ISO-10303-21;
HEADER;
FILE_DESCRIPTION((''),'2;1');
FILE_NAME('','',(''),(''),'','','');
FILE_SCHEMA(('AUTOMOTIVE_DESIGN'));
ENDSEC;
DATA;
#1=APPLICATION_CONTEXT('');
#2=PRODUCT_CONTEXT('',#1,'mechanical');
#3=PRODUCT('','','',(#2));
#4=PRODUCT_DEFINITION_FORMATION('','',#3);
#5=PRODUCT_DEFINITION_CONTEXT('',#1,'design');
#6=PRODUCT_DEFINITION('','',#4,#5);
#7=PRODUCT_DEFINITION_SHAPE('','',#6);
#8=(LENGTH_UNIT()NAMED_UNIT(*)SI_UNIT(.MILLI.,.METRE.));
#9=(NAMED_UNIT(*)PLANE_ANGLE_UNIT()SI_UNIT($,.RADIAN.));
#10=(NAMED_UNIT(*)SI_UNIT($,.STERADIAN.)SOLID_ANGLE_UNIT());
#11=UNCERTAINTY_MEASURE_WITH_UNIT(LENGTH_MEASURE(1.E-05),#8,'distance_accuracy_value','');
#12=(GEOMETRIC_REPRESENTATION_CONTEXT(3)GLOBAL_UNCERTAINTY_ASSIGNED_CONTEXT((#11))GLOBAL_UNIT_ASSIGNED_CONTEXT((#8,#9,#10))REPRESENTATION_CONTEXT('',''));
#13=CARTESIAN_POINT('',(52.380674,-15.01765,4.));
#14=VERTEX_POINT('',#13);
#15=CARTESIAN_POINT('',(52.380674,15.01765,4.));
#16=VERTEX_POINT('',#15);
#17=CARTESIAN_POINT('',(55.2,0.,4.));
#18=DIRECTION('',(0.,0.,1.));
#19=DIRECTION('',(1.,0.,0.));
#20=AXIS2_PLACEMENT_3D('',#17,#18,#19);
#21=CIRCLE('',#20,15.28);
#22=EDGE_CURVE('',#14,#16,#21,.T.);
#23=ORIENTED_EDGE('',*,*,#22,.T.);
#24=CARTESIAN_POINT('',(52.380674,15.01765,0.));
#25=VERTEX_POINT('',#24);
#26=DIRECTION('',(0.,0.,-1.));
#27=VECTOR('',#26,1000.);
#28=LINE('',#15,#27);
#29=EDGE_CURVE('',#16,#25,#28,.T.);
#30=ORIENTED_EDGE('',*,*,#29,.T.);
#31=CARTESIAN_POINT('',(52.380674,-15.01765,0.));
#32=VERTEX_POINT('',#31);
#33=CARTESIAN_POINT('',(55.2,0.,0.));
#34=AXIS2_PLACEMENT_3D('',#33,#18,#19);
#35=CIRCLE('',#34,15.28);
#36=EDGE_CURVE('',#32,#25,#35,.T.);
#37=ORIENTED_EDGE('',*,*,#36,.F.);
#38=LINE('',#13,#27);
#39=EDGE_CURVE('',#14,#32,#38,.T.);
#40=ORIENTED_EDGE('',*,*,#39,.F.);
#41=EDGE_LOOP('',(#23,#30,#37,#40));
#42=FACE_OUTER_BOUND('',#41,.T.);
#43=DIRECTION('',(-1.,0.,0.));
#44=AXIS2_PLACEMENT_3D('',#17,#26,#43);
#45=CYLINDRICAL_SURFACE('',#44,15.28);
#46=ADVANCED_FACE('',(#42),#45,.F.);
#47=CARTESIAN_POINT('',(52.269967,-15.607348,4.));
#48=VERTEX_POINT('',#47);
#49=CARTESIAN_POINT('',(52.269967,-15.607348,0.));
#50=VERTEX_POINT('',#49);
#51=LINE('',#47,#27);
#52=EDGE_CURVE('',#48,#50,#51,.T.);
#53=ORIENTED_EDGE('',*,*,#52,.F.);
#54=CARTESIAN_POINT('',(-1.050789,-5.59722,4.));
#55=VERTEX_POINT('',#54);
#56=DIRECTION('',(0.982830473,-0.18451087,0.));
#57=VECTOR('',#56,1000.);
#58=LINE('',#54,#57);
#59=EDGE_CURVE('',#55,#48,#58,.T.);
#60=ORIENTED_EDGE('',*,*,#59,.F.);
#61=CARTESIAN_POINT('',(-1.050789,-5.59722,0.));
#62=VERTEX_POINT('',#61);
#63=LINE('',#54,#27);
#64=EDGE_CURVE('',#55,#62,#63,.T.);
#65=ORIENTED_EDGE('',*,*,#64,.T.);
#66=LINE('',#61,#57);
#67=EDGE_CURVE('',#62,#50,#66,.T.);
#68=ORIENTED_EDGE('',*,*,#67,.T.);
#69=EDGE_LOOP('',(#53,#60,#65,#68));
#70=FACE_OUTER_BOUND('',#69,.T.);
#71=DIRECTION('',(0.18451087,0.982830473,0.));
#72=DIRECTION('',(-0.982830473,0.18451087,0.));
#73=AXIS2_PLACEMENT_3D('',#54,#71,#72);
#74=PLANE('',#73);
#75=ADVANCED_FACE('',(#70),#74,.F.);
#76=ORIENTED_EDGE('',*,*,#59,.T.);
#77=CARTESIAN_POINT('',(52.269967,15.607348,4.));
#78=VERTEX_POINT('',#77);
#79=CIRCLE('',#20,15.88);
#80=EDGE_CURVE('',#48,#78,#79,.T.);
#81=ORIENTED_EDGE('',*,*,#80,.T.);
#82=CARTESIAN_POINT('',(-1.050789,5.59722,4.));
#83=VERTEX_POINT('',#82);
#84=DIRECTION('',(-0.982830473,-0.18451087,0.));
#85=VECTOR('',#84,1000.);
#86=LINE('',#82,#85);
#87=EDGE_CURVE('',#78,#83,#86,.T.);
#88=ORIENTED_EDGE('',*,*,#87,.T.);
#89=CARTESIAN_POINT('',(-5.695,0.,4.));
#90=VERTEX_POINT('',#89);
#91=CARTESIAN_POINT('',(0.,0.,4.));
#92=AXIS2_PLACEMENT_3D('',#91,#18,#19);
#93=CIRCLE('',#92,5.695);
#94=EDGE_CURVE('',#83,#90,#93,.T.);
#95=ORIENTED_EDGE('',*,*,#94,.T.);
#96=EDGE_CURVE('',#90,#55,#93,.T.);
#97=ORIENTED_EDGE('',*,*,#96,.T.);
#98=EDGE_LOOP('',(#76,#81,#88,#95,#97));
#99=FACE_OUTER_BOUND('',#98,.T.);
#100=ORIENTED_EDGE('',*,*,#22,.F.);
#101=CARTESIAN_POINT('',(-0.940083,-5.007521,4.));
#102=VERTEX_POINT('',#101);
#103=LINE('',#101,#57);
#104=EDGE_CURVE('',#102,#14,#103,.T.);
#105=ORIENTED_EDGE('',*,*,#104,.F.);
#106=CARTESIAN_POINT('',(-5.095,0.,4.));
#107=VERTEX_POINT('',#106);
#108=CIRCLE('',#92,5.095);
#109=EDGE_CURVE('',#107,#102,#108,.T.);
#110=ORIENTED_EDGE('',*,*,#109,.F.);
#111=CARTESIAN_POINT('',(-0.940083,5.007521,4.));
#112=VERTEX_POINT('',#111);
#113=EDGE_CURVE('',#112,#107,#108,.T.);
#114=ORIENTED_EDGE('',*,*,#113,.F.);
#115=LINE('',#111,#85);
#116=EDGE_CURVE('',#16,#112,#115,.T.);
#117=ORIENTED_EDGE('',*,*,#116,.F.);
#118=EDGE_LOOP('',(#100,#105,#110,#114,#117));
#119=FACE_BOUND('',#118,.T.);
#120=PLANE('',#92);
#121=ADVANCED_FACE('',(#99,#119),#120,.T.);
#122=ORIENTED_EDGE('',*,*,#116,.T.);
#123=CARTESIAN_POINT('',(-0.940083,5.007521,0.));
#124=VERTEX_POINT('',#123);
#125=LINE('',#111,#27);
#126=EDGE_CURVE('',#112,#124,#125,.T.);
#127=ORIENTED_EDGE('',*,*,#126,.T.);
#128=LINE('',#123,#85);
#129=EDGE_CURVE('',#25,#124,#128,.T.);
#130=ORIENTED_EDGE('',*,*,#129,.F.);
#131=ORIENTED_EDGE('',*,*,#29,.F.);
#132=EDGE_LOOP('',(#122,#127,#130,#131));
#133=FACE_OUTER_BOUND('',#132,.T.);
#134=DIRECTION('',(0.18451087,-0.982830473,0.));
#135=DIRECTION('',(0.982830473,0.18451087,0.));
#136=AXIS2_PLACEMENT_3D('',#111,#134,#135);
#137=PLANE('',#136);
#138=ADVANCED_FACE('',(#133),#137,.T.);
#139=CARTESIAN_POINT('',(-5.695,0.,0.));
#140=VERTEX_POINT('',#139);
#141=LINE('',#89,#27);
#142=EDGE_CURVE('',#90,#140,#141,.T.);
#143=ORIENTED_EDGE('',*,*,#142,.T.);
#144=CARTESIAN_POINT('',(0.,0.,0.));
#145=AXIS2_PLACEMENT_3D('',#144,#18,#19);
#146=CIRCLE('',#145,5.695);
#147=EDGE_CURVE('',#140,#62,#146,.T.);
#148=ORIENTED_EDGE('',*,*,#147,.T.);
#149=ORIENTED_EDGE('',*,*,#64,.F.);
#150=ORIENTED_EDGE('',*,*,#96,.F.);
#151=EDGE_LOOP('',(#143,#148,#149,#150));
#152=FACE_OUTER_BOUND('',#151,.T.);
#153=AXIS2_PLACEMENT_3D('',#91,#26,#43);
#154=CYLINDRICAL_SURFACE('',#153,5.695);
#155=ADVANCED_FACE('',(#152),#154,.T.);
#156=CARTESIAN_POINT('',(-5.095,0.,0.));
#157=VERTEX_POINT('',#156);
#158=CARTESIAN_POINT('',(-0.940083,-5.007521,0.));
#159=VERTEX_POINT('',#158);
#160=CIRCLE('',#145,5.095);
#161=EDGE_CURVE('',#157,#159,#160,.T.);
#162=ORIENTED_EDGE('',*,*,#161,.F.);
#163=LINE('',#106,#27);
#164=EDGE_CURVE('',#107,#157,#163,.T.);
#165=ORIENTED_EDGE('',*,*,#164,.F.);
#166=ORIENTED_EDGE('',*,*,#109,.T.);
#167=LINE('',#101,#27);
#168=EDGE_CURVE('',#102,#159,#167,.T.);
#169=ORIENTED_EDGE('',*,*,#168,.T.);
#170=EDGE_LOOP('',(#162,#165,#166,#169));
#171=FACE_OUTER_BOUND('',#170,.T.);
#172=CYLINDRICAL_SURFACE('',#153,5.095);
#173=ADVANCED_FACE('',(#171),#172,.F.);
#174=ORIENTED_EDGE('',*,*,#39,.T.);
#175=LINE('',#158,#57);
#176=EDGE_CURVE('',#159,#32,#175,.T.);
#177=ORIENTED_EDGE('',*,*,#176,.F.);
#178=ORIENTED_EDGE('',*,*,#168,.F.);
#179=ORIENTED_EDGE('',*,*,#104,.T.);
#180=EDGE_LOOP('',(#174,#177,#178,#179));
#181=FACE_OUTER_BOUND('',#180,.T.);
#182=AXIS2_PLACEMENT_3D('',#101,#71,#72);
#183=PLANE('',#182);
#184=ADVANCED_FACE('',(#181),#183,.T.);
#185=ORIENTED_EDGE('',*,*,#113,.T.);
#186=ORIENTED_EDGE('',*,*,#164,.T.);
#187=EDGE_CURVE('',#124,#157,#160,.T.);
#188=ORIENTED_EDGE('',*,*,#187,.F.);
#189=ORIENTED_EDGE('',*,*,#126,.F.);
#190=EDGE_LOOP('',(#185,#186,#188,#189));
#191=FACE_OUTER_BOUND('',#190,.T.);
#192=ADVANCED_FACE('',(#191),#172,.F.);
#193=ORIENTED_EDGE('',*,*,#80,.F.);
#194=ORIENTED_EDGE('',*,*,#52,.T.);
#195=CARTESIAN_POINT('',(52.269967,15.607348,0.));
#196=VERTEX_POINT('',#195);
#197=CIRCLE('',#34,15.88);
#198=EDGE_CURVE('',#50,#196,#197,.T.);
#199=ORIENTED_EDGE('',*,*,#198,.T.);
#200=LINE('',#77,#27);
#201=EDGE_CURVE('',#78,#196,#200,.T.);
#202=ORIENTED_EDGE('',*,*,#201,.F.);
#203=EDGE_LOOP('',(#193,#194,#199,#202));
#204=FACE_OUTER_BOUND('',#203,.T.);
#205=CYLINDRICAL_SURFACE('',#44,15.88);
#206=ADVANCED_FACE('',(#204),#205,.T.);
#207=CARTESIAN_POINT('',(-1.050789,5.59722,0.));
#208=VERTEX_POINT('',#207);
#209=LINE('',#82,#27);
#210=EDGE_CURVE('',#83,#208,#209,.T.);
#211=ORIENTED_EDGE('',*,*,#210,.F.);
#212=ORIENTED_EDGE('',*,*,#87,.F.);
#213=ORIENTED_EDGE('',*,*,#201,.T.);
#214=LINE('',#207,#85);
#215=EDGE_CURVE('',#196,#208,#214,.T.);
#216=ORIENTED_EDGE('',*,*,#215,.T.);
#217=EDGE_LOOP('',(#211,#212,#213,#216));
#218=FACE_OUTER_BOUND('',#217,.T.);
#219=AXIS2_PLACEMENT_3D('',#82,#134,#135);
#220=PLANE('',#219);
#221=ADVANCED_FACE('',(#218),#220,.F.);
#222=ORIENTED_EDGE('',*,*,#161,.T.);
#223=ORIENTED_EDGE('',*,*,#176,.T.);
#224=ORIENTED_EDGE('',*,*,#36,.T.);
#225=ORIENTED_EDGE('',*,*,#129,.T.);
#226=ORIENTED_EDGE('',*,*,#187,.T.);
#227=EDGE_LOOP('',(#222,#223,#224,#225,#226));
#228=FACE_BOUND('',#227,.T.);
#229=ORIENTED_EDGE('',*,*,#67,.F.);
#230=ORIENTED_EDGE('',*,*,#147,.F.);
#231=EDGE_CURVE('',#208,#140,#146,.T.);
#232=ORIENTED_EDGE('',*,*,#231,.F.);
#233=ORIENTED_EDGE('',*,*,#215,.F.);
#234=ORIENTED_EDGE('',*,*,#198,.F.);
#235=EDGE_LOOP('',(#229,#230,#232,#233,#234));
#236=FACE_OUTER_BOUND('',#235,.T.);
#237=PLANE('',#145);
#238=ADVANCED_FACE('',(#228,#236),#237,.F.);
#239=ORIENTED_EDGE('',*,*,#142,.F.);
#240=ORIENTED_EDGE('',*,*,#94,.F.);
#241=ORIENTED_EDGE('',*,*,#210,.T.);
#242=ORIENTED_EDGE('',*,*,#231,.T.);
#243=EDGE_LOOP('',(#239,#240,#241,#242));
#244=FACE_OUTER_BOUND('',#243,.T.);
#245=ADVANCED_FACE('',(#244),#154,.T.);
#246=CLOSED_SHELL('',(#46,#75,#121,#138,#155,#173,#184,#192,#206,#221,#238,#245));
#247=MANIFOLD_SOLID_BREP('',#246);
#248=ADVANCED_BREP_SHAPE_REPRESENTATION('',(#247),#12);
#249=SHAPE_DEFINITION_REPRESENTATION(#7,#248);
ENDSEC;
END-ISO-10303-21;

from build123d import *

# Parameters (mm, degrees)
BOSS_EXTRUDE1_DEPTH = 4


with BuildPart() as part:
    # Sketch1 → Boss-Extrude1 (new body)
    with BuildSketch(Plane.XY):
        with BuildLine():
            Line((-1.050789402, -5.597219545), (52.269967391, -15.607347914))
            ThreePointArc((52.269967391, -15.607347914), (71.08, 0), (52.269967391, 15.607347914))
            Line((52.269967391, 15.607347914), (-1.050789402, 5.597219545))
            ThreePointArc((-1.050789402, 5.597219545), (-5.695, 0), (-1.050789402, -5.597219545))
        make_face()
        with BuildLine():
            Line((-0.94008288, 5.007521261), (52.380673913, 15.01764963))
            ThreePointArc((52.380673913, 15.01764963), (70.48, 0), (52.380673913, -15.01764963))
            Line((52.380673913, -15.01764963), (-0.94008288, -5.007521261))
            ThreePointArc((-0.94008288, -5.007521261), (-5.095, 0), (-0.94008288, 5.007521261))
        make_face(mode=Mode.SUBTRACT)
    extrude(amount=BOSS_EXTRUDE1_DEPTH)


solid = part.part
